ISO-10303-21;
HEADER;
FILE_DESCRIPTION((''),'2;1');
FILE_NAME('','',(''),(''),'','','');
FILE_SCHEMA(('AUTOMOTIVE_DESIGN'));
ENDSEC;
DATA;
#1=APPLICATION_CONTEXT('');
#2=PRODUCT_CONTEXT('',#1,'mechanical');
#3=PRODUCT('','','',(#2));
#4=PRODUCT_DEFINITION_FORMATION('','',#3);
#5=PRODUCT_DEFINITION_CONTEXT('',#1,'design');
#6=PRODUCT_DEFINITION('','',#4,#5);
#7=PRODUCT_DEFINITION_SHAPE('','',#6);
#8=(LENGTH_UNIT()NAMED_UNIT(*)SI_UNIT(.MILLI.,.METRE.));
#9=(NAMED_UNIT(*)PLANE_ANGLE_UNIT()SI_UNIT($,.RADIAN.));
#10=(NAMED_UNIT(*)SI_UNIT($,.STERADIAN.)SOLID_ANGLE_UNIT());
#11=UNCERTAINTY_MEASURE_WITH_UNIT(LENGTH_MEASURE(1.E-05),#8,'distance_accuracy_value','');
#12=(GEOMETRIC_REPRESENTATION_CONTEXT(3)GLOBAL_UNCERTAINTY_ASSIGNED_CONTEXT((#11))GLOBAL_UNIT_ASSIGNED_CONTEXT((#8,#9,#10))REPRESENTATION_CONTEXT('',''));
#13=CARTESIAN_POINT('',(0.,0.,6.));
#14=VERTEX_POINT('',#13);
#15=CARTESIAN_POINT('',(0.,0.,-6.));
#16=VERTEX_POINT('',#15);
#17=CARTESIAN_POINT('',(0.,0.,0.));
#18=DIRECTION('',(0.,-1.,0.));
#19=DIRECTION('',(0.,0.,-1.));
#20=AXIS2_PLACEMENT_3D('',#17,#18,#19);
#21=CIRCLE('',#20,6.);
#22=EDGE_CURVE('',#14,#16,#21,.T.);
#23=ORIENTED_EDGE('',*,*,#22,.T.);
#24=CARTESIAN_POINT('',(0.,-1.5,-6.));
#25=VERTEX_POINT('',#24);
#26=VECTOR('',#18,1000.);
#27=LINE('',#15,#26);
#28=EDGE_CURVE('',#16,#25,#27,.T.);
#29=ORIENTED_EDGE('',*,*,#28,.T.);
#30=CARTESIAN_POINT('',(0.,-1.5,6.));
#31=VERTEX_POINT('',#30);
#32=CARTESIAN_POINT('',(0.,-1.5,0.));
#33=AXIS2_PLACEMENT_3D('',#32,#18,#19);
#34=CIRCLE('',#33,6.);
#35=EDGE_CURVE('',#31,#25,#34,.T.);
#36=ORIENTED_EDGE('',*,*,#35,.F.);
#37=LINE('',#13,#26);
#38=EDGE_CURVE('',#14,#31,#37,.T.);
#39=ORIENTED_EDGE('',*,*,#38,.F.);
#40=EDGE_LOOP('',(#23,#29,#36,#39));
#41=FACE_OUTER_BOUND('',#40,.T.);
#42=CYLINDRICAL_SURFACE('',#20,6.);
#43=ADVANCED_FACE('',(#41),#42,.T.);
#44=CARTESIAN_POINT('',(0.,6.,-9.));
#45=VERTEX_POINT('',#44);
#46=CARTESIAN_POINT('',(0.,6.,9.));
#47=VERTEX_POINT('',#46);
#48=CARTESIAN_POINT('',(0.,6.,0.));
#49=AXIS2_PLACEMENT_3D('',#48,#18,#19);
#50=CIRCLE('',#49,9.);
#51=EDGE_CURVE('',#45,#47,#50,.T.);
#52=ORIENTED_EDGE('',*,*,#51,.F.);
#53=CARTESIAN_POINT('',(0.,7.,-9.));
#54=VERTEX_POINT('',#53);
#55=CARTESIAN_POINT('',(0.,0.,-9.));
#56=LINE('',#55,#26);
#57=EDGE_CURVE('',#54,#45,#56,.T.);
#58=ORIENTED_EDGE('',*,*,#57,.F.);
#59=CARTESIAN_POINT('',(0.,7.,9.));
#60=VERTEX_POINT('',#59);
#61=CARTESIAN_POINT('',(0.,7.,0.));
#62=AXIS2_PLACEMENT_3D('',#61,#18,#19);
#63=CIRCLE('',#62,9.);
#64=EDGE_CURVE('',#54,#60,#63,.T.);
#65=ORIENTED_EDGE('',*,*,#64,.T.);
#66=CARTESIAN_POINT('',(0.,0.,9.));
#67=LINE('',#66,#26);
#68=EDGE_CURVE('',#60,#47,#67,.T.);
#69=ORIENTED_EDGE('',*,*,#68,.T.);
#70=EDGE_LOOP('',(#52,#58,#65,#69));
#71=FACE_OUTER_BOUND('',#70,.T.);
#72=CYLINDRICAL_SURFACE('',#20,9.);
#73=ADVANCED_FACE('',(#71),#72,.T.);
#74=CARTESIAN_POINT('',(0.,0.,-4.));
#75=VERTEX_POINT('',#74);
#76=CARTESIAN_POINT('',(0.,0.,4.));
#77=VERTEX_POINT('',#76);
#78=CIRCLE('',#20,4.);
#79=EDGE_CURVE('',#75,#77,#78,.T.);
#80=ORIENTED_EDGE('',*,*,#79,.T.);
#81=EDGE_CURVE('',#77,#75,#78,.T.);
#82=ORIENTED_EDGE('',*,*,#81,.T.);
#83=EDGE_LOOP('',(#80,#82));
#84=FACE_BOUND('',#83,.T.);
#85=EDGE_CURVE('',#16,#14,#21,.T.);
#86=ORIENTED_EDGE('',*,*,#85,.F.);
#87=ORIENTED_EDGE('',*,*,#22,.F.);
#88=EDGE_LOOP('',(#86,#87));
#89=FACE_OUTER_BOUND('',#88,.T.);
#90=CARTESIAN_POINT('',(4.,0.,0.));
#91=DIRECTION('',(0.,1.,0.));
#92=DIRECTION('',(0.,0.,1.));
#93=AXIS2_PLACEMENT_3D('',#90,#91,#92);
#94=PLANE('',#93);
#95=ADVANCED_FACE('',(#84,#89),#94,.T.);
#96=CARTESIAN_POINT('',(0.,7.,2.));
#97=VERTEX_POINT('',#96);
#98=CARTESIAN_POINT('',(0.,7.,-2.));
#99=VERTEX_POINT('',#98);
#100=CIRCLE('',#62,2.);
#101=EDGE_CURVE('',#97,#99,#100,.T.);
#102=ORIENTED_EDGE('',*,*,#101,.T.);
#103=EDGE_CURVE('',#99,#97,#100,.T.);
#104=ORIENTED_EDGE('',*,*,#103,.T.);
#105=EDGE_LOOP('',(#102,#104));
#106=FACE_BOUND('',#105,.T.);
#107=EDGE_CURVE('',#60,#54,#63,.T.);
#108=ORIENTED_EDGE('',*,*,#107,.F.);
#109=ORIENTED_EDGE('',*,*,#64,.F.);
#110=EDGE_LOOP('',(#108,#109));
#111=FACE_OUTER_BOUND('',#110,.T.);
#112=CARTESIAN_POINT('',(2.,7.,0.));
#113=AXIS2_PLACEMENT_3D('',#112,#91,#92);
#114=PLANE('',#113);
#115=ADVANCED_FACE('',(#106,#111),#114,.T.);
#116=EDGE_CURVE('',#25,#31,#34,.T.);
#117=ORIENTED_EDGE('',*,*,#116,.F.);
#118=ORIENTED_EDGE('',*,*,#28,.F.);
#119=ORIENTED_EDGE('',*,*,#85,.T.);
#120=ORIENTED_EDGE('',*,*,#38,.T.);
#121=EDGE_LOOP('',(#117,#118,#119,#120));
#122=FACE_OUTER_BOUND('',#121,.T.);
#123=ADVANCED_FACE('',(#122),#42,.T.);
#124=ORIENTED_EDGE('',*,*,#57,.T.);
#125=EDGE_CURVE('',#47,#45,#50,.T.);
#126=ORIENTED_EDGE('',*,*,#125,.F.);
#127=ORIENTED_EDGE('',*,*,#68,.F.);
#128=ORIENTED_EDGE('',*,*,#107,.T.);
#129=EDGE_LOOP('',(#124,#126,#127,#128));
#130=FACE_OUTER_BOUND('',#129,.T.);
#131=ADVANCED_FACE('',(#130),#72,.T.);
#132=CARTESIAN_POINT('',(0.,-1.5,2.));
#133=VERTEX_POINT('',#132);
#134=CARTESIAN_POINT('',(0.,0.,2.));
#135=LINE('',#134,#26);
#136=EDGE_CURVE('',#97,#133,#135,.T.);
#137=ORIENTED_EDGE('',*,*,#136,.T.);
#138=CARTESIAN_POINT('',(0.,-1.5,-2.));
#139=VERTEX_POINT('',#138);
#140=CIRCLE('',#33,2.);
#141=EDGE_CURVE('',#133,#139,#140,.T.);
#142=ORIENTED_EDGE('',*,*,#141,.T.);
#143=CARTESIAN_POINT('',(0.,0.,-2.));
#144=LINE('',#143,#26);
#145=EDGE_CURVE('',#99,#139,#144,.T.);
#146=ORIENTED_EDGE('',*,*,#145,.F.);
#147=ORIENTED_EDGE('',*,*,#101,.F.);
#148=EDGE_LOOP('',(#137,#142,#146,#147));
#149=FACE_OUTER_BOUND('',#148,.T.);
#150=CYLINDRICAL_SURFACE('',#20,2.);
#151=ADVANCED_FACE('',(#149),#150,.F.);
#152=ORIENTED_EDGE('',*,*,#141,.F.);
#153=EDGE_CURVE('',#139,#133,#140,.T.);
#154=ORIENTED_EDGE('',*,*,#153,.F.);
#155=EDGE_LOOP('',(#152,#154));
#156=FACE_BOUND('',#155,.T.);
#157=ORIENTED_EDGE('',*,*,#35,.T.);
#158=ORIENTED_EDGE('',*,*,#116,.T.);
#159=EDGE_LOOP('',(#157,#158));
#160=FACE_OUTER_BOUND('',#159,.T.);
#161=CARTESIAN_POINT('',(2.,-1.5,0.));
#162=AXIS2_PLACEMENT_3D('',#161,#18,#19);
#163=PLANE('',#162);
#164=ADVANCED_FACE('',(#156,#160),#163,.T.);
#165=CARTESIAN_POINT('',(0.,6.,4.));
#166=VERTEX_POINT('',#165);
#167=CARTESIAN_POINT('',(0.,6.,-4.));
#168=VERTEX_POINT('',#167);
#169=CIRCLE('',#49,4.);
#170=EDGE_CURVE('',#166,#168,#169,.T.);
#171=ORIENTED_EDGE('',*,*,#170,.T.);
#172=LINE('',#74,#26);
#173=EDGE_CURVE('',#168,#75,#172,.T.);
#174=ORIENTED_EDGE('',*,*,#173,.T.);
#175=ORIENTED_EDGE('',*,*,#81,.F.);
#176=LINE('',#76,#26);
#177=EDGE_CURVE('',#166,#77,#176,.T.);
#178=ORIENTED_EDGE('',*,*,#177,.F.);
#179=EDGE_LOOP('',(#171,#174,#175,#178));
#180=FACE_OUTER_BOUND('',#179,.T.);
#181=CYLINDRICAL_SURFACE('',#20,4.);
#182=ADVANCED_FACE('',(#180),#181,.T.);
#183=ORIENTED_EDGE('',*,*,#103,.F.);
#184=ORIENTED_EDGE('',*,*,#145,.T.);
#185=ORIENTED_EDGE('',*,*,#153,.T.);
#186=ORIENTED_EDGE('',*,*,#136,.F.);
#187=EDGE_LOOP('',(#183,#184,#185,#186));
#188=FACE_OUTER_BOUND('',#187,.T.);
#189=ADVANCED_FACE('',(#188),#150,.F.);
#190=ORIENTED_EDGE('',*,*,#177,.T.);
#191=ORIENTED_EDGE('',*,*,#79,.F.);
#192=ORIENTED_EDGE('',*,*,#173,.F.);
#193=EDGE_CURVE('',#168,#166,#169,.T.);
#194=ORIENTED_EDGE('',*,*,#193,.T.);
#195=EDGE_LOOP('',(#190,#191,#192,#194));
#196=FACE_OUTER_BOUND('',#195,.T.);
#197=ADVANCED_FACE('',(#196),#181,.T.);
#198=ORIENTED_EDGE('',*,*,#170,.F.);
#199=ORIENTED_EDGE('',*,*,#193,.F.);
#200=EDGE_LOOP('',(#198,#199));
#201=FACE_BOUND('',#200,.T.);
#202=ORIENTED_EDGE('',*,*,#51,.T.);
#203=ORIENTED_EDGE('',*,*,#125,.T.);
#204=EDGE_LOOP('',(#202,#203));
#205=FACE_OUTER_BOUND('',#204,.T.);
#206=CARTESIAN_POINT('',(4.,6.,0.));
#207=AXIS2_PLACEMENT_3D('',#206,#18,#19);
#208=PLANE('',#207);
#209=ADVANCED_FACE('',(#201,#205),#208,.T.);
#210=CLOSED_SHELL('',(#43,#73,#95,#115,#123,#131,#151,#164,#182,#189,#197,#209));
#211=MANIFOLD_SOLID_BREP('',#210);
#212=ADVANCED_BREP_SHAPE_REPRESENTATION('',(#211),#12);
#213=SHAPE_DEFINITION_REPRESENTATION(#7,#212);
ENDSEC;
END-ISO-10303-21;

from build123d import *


with BuildPart() as part:
    # Sketch1 → Revolve1 (revolve)
    with BuildSketch(Plane.XY, mode=Mode.PRIVATE) as revolve1_sk:
        Polygon((2, 7), (2, -1.5), (6, -1.5), (6, 0), (4, 0), (4, 6), (9, 6), (9, 7), align=None)
    revolve(revolve1_sk.sketch.rotate(Axis((0, 0, 0), (0, 1, 0)), 90), axis=Axis((0, 0, 0), (0, 1, 0)))


solid = part.part
